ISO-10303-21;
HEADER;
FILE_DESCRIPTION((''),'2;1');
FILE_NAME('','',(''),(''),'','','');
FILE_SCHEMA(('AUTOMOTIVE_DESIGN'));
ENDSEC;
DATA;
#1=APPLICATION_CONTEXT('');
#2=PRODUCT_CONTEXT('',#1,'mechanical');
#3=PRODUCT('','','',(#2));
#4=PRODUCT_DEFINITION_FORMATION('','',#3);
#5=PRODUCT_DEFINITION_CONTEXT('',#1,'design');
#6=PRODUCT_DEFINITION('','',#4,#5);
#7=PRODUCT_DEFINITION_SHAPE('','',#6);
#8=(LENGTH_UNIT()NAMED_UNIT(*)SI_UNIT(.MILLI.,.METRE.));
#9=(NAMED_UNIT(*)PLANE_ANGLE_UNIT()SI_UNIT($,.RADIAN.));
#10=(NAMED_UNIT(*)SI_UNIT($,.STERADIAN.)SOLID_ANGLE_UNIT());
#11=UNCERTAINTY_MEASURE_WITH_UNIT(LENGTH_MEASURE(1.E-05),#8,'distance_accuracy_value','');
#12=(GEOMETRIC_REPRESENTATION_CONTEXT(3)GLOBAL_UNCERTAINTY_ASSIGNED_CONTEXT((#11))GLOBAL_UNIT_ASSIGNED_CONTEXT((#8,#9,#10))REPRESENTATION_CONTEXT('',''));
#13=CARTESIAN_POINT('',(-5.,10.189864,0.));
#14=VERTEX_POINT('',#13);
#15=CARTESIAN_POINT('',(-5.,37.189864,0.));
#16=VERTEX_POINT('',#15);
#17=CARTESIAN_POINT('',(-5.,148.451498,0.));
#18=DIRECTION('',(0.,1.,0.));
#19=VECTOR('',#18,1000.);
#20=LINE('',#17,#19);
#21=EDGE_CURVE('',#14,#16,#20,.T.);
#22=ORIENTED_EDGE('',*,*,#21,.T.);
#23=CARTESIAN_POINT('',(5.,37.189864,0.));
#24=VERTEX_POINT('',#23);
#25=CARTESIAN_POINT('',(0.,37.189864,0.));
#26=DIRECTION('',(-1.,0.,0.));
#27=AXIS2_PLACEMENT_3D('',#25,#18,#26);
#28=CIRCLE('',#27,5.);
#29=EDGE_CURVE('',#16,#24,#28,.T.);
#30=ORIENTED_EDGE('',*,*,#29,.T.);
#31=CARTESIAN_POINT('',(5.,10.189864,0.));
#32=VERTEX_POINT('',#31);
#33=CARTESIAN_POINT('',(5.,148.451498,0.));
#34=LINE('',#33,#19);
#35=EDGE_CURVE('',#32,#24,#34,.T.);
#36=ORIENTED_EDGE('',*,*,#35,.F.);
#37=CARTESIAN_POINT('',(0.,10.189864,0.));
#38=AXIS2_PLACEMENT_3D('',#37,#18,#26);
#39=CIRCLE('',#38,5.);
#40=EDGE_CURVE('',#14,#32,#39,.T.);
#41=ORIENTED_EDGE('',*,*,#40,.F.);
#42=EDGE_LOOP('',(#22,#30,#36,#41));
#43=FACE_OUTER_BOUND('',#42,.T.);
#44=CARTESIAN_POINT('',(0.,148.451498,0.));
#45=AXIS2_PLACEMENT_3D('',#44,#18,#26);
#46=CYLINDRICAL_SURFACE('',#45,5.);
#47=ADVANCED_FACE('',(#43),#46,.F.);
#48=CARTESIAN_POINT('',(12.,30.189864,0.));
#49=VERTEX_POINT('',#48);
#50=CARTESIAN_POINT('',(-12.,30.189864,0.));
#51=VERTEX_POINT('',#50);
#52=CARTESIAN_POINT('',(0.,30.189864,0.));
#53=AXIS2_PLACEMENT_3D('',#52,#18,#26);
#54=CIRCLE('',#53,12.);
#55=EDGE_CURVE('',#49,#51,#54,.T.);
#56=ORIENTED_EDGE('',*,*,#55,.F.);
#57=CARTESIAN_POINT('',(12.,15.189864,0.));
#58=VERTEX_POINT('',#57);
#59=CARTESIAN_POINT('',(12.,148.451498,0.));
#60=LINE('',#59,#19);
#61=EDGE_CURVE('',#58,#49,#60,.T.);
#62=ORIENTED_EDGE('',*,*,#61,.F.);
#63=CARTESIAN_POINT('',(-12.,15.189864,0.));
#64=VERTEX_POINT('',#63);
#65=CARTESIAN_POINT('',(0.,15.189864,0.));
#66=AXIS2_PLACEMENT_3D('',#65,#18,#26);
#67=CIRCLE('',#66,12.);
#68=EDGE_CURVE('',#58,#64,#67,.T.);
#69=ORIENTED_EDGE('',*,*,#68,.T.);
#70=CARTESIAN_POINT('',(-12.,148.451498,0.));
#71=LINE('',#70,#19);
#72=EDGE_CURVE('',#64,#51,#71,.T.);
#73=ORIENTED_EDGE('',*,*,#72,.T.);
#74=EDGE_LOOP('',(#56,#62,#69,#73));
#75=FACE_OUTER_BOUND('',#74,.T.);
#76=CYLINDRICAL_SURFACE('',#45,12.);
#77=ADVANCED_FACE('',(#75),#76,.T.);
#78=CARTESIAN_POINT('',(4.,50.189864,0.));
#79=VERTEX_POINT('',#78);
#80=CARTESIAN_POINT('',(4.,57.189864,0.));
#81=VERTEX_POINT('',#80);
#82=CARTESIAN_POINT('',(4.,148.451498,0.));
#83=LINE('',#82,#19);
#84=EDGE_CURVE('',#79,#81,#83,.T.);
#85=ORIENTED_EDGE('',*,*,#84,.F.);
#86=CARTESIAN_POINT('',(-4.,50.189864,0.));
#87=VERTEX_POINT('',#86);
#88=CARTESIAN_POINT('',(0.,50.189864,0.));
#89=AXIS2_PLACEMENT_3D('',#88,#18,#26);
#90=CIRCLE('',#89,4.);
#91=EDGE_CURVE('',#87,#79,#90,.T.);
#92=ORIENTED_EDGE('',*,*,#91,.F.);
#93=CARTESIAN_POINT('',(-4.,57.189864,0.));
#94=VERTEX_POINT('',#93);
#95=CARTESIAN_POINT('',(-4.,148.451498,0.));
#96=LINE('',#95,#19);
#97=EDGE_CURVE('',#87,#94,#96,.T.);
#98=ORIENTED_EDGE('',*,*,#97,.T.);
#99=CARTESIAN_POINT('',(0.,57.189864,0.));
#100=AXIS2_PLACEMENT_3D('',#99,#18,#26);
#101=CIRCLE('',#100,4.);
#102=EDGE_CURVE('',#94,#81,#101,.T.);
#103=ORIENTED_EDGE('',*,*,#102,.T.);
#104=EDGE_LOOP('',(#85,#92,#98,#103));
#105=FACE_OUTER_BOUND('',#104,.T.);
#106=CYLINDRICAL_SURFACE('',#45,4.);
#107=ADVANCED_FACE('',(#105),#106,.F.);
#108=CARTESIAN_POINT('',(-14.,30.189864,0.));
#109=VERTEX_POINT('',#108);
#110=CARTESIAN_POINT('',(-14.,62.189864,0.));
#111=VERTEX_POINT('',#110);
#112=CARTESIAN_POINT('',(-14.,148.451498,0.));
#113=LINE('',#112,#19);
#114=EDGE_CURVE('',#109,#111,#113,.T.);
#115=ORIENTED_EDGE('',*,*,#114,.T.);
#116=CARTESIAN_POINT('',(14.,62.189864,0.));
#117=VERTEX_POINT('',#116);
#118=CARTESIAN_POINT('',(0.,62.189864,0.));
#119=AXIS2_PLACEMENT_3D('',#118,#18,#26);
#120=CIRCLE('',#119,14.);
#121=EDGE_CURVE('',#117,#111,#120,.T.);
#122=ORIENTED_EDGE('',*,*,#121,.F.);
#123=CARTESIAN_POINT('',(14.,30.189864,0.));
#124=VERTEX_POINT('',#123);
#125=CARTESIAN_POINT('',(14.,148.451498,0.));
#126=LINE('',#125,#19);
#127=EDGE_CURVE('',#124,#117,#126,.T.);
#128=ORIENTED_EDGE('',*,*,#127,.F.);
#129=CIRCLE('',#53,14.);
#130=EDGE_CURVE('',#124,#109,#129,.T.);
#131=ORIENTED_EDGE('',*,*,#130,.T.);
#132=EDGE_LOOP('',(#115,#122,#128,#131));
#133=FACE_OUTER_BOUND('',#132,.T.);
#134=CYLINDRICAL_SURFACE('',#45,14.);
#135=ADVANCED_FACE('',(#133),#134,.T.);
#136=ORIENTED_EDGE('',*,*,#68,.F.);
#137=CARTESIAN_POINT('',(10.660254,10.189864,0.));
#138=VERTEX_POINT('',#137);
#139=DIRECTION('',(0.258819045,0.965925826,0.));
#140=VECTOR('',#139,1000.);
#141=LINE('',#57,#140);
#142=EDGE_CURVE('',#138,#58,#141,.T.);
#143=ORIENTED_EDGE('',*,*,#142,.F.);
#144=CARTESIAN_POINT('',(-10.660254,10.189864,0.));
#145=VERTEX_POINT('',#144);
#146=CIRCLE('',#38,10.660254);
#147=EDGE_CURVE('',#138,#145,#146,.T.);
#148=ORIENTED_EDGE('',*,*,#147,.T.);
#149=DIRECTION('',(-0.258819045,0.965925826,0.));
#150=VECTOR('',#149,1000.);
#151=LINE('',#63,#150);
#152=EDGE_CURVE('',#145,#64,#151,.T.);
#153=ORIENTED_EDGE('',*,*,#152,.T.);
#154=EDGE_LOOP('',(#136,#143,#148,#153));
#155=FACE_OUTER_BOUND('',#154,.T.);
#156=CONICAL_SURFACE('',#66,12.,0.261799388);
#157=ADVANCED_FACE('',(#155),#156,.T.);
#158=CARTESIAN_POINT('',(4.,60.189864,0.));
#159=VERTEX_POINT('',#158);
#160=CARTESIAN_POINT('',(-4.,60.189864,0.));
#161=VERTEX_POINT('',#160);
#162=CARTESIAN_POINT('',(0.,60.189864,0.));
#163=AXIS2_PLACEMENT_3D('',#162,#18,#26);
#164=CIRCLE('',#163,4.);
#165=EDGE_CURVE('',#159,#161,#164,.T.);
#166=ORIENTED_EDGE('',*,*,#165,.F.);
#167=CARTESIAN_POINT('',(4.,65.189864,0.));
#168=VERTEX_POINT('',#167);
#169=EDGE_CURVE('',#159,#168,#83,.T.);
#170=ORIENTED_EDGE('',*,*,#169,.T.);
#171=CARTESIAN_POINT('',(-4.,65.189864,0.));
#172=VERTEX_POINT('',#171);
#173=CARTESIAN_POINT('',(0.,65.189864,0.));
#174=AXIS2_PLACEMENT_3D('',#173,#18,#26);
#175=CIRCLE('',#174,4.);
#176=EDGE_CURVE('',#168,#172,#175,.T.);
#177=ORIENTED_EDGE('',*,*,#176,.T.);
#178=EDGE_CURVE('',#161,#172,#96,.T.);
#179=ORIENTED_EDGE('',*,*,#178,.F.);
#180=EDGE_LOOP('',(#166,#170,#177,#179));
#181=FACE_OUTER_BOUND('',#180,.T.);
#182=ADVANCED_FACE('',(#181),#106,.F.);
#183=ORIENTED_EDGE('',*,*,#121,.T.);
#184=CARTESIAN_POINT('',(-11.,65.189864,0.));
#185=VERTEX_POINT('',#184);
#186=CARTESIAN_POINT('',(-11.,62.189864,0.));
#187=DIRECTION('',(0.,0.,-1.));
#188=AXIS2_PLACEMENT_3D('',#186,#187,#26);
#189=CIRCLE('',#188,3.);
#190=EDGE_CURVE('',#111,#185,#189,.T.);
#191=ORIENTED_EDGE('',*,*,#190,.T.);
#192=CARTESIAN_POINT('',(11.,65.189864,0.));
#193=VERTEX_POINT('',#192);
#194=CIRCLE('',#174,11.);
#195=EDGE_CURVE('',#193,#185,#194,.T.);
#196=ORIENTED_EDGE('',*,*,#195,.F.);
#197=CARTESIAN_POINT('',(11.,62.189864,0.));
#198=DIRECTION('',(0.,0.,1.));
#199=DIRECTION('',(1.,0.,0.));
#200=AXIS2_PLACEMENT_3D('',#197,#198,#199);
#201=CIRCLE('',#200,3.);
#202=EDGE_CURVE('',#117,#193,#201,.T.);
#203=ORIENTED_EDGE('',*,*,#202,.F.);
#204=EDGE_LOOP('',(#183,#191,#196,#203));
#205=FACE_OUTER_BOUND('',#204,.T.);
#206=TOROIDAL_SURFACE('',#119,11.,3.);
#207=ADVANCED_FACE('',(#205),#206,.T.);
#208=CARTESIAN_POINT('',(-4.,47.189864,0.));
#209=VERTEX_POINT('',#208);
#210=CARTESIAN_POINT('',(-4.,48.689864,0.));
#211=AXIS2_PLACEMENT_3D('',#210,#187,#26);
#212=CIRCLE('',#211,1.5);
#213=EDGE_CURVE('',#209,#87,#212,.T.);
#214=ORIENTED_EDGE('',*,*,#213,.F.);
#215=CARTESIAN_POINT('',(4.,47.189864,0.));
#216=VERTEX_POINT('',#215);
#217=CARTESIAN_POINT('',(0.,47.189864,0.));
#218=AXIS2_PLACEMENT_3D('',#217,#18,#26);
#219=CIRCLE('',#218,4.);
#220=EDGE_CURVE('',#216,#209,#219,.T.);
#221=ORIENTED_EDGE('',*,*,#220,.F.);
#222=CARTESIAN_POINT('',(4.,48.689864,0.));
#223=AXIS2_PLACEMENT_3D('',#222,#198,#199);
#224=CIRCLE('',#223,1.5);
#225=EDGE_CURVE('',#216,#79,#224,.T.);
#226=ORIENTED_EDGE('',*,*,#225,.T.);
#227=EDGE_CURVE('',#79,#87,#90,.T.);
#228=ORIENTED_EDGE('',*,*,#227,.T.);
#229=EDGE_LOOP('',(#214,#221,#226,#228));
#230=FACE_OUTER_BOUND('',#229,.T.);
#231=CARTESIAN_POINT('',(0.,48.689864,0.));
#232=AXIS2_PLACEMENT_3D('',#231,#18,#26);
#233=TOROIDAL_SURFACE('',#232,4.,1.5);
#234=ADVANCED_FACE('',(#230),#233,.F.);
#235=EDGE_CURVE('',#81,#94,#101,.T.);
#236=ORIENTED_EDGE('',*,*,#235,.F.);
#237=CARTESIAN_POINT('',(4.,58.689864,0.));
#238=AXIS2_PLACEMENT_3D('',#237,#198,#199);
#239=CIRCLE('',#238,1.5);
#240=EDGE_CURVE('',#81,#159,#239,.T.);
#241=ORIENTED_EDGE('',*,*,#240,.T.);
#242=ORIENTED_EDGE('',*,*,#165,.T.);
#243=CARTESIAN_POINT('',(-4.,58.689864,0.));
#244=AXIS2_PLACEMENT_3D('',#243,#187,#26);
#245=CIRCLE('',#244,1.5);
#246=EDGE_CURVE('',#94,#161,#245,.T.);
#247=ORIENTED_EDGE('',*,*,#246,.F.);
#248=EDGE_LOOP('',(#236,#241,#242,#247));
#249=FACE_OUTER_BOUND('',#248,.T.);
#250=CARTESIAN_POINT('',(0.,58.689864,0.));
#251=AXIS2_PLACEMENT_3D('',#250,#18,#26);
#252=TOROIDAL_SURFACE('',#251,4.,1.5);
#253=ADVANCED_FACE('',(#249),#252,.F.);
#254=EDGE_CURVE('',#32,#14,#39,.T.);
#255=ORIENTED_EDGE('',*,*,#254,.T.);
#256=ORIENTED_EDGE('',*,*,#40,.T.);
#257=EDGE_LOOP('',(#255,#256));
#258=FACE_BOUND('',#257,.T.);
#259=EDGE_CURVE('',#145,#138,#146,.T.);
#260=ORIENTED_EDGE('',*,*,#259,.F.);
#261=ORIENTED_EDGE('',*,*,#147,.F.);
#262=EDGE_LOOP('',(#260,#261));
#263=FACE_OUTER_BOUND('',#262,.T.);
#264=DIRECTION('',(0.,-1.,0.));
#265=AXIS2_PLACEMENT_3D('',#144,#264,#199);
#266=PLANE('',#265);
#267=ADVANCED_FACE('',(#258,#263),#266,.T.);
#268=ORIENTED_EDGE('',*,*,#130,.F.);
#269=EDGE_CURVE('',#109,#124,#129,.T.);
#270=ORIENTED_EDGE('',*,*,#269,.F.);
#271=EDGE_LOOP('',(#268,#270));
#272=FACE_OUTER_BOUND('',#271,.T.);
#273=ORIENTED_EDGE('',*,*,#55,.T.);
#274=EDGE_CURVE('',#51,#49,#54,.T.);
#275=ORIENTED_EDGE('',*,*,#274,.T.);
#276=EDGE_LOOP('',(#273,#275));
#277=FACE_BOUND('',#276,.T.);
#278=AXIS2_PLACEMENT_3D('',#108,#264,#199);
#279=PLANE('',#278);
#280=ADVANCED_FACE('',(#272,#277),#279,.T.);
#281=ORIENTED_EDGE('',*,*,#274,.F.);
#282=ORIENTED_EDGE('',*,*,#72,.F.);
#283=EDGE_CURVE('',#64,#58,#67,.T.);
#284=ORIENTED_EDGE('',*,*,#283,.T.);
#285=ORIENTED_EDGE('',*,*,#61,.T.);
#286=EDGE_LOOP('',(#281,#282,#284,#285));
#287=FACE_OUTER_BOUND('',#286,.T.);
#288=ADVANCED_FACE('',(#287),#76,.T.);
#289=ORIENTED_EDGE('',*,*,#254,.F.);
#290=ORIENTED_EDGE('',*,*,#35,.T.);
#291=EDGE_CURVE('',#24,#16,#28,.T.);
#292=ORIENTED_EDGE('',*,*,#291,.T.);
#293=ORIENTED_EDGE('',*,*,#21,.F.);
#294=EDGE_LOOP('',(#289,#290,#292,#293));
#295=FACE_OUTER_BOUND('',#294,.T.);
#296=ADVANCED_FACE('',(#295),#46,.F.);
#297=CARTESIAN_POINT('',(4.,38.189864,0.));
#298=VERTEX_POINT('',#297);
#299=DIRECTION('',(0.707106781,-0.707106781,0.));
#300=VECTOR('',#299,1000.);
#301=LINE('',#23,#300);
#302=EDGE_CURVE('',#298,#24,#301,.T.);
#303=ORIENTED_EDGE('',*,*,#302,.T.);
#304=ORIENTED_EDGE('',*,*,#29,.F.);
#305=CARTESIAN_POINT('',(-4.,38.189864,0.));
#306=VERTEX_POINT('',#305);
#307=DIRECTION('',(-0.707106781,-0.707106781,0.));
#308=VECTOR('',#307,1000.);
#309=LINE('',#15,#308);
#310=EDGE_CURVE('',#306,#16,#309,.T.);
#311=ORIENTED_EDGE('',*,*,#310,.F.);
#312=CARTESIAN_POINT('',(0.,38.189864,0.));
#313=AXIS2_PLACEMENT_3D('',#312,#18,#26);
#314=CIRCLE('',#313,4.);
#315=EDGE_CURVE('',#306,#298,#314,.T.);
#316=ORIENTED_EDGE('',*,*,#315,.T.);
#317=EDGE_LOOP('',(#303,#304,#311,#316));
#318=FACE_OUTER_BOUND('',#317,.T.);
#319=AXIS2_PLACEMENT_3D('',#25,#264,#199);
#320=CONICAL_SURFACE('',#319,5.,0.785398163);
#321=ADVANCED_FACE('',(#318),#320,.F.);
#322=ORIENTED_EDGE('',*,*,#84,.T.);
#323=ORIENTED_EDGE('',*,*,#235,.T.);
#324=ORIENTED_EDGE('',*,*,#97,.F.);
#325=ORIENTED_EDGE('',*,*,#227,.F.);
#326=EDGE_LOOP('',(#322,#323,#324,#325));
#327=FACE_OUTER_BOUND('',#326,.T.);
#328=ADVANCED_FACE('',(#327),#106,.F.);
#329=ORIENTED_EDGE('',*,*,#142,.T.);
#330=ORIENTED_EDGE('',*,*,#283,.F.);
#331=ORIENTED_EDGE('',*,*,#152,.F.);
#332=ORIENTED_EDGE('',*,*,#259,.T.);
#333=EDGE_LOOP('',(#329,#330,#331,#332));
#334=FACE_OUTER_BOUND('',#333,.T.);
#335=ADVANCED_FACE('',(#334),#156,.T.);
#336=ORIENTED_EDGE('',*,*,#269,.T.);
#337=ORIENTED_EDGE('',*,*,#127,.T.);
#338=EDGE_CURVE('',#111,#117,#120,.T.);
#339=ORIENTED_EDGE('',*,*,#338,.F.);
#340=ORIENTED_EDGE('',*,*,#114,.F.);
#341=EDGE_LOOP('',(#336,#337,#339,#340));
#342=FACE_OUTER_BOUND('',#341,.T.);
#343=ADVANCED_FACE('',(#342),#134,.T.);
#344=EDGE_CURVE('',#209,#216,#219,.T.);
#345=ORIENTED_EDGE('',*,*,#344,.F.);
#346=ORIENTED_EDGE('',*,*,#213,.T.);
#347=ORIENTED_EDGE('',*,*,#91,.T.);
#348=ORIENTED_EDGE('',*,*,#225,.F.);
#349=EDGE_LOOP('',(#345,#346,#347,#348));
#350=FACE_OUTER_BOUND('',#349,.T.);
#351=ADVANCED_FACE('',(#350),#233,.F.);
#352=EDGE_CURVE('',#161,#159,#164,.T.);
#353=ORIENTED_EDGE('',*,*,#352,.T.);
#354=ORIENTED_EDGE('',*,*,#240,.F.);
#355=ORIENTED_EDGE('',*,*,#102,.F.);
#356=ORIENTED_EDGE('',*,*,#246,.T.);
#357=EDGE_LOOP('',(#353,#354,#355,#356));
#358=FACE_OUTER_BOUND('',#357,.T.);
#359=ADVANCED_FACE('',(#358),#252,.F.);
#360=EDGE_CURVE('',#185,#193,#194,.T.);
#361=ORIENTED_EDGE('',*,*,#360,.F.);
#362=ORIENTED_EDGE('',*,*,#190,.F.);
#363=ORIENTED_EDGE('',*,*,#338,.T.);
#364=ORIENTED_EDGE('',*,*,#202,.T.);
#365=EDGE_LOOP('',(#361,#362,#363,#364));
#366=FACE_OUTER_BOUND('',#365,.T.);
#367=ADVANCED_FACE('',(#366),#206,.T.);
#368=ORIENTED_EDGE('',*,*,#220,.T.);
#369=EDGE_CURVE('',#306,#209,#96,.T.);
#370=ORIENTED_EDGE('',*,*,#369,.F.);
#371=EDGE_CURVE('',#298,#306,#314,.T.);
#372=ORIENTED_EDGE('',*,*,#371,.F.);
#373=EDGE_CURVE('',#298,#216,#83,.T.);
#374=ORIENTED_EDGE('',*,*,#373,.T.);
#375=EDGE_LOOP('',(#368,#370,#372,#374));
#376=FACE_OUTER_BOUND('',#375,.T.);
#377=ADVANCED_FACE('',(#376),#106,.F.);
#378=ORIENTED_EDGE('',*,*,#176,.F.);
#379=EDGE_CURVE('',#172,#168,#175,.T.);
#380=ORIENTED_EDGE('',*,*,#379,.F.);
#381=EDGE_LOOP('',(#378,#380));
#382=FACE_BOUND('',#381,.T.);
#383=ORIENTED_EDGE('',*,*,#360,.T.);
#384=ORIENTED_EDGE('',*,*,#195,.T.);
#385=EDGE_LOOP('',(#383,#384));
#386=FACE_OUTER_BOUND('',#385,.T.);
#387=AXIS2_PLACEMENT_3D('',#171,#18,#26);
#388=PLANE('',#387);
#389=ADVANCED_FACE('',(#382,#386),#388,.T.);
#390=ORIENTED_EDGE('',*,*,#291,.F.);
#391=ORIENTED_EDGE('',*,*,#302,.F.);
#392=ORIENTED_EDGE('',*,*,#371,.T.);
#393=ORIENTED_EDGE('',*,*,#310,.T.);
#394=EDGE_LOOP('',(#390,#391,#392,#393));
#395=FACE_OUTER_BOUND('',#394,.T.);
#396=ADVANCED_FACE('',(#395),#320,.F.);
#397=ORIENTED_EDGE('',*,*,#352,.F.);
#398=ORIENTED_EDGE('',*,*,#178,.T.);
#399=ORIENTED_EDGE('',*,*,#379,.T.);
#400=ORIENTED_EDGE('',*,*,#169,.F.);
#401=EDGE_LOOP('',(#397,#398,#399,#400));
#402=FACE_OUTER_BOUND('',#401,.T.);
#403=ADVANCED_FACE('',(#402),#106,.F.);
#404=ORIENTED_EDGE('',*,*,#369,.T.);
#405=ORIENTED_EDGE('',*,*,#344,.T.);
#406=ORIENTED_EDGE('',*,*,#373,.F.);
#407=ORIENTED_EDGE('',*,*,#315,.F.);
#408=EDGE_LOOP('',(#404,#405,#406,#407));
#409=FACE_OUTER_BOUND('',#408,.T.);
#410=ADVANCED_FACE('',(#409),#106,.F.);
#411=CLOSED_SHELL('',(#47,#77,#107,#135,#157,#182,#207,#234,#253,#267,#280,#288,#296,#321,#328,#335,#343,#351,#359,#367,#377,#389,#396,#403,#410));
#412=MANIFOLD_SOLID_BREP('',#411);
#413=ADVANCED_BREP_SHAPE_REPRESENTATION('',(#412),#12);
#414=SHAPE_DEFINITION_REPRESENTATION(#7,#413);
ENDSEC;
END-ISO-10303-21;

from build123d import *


with BuildPart() as part:
    # Pin Revolve Profile → Pin Body Revolve (revolve)
    with BuildSketch(Plane.XY):
        with BuildLine():
            Line((-4, 60.189864048), (-4, 65.189864048))
            Line((-4, 65.189864048), (-11, 65.189864048))
            ThreePointArc((-11, 65.189864048), (-13.121320344, 64.311184392), (-14, 62.189864048))
            Line((-14, 62.189864048), (-14, 30.189864048))
            Line((-14, 30.189864048), (-12, 30.189864048))
            Line((-12, 30.189864048), (-12, 15.189864048))
            Line((-12, 15.189864048), (-10.660254038, 10.189864048))
            Line((-10.660254038, 10.189864048), (-5, 10.189864048))
            Line((-5, 10.189864048), (-5, 37.189864048))
            Line((-5, 37.189864048), (-4, 38.189864048))
            Line((-4, 38.189864048), (-4, 47.189864048))
            ThreePointArc((-4, 47.189864048), (-5.5, 48.689864048), (-4, 50.189864048))
            Line((-4, 50.189864048), (-4, 57.189864048))
            ThreePointArc((-4, 57.189864048), (-5.5, 58.689864048), (-4, 60.189864048))
        make_face()
    revolve(axis=Axis((0, 148.451497923, 0), (0, -1, 0)))


solid = part.part
